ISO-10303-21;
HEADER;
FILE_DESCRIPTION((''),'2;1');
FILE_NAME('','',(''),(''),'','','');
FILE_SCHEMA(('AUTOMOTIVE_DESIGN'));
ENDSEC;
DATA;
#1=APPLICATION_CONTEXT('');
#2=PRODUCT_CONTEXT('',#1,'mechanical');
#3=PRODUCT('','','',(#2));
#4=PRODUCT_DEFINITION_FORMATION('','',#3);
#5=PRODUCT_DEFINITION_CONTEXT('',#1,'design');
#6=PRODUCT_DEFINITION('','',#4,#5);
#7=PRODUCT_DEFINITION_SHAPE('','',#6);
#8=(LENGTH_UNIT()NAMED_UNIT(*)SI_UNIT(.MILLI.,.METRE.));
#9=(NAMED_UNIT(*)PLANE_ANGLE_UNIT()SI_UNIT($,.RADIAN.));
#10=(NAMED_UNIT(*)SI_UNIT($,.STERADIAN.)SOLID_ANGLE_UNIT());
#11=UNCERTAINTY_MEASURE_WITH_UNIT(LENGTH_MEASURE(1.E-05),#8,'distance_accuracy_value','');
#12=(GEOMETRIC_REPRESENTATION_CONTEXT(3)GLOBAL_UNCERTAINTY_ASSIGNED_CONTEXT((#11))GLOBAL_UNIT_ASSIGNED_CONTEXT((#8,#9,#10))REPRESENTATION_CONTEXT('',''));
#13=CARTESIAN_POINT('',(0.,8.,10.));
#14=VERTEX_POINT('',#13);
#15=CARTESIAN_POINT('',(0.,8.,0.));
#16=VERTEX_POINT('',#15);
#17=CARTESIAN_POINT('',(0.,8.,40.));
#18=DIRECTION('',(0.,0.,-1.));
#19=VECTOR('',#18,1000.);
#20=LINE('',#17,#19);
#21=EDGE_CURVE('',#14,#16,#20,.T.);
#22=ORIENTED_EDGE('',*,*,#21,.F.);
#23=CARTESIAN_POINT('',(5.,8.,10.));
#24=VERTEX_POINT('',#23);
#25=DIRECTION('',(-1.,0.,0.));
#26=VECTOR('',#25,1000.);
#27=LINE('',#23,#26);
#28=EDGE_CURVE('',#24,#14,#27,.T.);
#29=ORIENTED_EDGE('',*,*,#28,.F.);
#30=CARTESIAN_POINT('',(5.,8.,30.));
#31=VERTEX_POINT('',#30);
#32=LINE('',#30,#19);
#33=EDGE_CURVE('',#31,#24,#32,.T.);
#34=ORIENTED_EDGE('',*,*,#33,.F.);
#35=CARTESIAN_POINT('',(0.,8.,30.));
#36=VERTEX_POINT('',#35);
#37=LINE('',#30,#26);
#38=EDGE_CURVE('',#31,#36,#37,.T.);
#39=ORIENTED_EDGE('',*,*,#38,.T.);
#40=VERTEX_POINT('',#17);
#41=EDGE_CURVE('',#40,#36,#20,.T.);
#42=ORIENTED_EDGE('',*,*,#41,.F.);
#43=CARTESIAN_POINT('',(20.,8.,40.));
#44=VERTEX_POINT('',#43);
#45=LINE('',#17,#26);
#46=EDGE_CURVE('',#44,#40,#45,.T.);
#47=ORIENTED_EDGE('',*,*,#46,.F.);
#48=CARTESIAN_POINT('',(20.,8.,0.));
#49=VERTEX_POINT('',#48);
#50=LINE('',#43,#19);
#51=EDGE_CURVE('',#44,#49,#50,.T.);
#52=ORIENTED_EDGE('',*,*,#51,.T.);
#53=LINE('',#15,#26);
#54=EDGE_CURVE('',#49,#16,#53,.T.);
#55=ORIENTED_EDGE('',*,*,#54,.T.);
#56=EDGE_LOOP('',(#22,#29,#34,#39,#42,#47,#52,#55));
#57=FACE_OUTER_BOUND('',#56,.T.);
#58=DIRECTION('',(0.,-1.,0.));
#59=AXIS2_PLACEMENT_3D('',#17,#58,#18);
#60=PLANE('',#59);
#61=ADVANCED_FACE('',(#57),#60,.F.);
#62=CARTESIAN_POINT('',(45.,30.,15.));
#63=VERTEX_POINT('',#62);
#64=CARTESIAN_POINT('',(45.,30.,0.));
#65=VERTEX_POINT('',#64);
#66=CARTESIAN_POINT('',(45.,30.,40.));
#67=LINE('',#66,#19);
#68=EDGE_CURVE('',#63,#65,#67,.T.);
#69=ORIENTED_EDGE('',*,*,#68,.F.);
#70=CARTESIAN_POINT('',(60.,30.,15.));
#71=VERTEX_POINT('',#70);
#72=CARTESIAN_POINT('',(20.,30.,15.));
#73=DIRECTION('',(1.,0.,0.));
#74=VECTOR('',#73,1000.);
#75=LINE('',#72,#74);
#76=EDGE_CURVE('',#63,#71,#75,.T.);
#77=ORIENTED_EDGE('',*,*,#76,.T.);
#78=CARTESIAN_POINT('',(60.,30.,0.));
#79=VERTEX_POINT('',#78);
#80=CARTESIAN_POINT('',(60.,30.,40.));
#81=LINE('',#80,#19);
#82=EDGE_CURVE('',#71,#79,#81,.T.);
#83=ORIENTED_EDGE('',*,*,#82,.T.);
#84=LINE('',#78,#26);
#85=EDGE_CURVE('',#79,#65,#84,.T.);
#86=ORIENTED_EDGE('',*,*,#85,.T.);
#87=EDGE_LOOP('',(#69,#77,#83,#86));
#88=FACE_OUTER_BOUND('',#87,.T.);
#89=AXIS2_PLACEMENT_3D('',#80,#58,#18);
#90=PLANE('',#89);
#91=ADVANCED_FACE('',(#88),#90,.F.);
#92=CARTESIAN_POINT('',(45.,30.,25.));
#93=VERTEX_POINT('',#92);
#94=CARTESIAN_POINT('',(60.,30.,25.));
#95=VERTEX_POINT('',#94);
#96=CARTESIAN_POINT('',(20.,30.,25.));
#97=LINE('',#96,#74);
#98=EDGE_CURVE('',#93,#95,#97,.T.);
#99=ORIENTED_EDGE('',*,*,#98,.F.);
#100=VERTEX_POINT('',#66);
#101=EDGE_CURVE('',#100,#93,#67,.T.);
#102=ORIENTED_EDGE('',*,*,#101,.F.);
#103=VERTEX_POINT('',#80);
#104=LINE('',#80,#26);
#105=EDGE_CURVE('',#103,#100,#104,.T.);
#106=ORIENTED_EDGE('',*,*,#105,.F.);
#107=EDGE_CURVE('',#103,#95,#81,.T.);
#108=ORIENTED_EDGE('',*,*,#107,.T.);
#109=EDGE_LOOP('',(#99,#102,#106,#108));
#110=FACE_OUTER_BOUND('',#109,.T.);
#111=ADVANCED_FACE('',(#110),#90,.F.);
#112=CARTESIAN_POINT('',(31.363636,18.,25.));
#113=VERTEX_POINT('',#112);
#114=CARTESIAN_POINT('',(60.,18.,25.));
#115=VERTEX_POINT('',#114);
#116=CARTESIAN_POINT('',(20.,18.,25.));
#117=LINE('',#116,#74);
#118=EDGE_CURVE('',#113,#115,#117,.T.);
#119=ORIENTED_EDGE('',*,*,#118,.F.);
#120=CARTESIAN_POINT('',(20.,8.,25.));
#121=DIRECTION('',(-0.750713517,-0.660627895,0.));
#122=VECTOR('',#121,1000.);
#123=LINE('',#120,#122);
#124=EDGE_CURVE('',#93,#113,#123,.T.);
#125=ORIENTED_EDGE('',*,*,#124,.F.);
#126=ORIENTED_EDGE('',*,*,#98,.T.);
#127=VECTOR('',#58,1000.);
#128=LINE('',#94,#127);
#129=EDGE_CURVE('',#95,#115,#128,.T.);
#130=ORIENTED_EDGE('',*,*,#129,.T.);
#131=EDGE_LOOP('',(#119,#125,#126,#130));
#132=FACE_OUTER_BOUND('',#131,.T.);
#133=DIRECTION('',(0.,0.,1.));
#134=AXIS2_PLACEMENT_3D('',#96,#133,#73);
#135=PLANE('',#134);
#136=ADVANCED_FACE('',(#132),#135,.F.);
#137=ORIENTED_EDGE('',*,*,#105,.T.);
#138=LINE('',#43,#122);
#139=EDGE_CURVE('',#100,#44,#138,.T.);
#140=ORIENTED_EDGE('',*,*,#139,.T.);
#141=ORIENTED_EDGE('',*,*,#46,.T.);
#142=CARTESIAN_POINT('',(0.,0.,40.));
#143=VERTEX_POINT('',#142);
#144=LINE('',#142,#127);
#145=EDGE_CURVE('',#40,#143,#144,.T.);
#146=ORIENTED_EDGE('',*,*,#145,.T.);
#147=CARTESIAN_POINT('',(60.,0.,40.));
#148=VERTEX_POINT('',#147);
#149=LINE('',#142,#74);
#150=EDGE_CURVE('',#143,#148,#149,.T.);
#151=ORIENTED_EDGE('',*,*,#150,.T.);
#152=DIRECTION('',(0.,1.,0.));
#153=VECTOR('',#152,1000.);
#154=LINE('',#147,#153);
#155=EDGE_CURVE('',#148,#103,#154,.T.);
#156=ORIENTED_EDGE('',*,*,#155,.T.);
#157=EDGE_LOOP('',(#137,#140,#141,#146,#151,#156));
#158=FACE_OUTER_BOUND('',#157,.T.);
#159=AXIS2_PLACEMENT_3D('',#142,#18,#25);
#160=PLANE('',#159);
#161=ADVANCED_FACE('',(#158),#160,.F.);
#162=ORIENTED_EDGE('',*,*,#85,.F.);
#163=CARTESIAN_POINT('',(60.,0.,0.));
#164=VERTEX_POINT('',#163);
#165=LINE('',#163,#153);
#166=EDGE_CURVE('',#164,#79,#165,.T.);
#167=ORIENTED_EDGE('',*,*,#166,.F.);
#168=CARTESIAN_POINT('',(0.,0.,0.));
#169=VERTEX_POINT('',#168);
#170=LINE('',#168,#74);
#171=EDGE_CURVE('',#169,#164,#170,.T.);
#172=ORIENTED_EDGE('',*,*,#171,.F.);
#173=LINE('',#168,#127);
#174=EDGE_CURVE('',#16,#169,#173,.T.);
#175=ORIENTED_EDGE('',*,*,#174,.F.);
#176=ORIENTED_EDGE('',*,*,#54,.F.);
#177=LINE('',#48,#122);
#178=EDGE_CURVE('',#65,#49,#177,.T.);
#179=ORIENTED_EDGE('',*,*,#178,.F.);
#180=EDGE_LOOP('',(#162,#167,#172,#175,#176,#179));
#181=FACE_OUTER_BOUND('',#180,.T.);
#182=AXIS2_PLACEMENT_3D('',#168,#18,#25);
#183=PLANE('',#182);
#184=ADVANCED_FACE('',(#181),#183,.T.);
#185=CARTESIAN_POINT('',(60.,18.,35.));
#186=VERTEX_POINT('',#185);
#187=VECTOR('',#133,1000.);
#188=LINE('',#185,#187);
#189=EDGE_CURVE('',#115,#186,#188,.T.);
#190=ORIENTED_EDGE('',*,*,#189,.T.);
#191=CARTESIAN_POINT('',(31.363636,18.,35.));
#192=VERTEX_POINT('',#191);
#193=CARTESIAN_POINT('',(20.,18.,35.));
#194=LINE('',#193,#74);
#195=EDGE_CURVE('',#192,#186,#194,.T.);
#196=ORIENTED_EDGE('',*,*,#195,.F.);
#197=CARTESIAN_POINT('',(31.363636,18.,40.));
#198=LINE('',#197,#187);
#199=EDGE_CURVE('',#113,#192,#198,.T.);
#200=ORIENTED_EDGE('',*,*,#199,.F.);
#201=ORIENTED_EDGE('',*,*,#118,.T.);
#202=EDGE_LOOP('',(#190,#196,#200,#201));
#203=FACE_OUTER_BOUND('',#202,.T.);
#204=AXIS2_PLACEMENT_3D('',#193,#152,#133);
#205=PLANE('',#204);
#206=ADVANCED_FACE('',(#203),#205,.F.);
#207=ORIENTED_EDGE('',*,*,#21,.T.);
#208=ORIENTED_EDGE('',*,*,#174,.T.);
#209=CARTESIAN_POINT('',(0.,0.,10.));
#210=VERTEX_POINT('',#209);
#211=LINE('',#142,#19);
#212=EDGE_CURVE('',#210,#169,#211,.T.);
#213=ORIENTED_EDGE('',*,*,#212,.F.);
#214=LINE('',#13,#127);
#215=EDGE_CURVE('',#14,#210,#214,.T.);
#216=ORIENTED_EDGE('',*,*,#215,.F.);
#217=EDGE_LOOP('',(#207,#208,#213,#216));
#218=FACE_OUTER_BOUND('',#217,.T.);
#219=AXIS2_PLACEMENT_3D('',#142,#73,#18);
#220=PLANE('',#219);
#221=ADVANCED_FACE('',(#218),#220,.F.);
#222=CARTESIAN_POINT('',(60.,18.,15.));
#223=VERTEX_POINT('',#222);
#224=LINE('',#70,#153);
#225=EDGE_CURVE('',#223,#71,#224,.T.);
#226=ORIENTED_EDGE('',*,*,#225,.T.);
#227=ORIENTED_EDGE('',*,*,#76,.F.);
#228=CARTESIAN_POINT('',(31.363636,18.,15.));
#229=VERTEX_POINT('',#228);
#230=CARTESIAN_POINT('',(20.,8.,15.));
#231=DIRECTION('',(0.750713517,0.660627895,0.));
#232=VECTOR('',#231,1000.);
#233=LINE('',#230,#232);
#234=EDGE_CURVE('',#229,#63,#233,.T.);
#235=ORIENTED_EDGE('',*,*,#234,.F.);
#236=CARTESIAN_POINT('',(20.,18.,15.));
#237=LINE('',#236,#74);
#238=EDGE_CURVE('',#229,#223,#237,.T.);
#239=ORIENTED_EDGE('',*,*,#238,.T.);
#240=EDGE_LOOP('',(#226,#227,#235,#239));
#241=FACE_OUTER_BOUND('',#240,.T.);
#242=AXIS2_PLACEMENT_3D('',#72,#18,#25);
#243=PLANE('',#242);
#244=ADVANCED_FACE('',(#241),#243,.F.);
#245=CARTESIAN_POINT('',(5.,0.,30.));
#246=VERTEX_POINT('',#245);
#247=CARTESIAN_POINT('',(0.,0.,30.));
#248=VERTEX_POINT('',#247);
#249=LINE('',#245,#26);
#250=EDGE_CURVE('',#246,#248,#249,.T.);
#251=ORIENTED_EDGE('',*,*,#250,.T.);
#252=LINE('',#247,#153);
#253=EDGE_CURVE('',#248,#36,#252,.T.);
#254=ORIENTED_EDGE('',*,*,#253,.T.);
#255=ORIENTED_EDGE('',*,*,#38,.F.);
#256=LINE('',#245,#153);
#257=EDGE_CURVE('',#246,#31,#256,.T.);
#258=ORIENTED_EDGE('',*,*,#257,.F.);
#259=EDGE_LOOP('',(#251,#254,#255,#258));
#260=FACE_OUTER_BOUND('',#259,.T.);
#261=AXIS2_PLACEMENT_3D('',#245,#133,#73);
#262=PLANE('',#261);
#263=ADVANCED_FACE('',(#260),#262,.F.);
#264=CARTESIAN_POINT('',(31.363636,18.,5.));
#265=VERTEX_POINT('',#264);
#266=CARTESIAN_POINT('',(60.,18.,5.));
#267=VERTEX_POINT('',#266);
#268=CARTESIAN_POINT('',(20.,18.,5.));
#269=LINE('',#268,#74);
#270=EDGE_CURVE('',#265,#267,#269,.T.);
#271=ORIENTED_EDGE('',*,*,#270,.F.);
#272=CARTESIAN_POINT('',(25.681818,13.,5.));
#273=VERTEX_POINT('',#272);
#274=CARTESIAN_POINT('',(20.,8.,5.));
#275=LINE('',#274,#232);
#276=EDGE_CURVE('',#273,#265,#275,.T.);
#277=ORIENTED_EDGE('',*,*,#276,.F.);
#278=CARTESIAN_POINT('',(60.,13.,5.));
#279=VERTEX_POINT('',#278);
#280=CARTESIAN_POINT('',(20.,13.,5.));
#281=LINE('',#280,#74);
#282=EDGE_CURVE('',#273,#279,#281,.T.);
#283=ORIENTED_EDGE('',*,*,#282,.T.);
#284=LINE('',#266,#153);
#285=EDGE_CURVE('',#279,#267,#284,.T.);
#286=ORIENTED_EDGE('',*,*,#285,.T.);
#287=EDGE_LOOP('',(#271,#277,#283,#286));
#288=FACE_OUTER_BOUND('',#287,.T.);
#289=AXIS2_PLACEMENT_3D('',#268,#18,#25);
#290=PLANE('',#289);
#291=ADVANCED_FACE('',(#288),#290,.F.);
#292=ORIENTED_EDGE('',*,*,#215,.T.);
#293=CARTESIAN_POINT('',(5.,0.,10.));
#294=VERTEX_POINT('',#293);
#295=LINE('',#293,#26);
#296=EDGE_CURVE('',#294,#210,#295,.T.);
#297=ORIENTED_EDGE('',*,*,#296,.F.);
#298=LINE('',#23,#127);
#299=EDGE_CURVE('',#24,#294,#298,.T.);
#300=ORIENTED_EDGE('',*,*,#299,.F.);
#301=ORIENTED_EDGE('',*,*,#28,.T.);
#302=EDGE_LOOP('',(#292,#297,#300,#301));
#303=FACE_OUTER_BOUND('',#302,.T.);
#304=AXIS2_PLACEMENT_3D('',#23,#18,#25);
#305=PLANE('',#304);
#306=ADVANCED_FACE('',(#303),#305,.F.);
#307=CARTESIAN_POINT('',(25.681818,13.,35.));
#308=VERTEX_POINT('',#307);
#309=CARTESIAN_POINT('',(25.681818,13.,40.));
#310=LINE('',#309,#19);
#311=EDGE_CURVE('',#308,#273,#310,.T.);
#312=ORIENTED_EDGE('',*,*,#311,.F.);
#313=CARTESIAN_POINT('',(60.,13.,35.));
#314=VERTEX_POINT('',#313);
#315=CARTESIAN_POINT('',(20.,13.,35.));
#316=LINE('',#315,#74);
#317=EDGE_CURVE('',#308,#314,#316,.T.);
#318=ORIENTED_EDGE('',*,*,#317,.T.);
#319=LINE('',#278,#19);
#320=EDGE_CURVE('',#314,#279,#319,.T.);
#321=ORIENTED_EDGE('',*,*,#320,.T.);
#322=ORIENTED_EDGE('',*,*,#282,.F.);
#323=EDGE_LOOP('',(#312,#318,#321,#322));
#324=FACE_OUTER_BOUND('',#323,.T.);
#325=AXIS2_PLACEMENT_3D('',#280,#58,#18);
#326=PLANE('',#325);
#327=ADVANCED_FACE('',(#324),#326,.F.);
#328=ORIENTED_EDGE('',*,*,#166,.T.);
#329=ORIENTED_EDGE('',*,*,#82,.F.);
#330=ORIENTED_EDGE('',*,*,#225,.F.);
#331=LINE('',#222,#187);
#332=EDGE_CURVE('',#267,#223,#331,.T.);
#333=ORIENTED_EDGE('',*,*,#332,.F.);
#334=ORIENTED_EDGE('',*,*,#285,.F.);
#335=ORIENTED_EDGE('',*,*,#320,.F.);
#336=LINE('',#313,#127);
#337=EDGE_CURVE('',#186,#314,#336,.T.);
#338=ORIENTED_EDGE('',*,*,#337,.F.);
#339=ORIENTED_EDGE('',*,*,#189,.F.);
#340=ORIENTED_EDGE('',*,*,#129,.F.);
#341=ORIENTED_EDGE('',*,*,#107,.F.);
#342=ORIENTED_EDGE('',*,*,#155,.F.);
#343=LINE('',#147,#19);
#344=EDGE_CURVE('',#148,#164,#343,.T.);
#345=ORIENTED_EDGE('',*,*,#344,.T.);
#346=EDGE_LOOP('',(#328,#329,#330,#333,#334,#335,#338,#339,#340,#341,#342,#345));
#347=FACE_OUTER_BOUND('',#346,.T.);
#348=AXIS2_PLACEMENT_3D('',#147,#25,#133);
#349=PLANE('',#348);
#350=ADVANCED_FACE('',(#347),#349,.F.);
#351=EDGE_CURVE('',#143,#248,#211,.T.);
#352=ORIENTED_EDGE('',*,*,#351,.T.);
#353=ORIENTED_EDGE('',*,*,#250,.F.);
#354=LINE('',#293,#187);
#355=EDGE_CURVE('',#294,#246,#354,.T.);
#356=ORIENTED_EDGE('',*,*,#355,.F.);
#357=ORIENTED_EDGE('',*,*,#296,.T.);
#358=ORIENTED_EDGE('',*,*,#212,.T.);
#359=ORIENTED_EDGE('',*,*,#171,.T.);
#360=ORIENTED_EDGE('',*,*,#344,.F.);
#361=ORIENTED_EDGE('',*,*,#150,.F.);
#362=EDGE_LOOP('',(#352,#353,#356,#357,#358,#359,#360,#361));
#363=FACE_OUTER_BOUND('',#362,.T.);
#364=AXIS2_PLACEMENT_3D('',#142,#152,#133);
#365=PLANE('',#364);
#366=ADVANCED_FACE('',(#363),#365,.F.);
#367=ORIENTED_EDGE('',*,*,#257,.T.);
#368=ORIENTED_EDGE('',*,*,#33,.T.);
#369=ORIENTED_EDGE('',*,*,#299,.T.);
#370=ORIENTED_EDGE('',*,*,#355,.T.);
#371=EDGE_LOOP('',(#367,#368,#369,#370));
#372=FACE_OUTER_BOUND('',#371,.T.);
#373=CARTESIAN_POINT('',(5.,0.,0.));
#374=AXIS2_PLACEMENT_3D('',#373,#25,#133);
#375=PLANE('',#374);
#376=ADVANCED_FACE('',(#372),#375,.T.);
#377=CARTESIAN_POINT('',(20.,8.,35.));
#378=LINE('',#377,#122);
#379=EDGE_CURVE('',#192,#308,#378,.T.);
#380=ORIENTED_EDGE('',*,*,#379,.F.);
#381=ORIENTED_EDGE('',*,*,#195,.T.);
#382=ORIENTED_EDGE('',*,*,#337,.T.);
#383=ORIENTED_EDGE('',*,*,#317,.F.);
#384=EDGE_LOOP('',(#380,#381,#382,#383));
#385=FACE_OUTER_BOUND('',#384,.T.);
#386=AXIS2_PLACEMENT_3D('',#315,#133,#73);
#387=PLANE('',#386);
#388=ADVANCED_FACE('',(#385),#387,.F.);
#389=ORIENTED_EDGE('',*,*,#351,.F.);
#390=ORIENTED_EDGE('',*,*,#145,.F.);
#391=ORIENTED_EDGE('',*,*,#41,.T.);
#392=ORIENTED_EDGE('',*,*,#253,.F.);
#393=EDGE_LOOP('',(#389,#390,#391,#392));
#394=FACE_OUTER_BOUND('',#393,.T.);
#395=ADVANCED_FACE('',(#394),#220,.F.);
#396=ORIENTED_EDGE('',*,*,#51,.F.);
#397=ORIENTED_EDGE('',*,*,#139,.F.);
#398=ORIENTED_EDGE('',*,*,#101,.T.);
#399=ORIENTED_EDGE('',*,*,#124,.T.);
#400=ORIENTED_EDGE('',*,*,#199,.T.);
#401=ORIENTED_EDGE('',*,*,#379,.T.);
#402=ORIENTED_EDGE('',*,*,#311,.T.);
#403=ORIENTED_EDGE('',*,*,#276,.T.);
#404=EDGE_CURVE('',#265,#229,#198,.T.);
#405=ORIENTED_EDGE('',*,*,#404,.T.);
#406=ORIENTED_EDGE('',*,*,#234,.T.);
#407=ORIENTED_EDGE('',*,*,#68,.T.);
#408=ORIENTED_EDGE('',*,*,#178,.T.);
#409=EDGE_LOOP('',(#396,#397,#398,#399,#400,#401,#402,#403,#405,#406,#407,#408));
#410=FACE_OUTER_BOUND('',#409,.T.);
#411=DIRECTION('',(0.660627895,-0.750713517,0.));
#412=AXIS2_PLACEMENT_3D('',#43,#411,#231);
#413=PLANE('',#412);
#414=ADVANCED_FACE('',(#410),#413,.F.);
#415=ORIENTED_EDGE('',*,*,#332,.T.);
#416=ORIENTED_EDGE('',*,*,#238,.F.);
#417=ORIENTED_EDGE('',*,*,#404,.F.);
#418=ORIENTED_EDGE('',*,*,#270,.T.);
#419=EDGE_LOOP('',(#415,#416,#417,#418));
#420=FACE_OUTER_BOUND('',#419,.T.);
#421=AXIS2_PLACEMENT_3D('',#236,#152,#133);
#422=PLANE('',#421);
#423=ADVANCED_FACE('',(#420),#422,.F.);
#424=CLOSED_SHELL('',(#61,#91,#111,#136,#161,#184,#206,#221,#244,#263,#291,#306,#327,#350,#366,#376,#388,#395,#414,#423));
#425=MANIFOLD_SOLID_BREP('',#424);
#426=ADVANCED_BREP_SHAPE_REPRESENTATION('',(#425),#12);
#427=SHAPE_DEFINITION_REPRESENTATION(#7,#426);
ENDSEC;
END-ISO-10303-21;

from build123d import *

# Parameters (mm, degrees)
ANGLED_BASE_BLOCK_DEPTH  = 40
GROOVE_CUT_5MM_DEPTH     = 5
T_SLOT_THROUGH_CUT_DEPTH = 40


with BuildPart() as part:
    # Base Profile Sketch → Angled Base Block (new body)
    with BuildSketch(Plane.XY):
        Polygon((0, 0), (60, 0), (60, 30), (45, 30), (20, 8), (0, 8), align=None)
    extrude(amount=ANGLED_BASE_BLOCK_DEPTH)

    # Groove Profile Sketch → Groove Cut 5mm (cut)
    with BuildSketch(Plane.ZY):
        Polygon((20, 8), (10, 8), (10, 0), (30, 0), (30, 8), align=None)
    extrude(amount=-GROOVE_CUT_5MM_DEPTH, mode=Mode.SUBTRACT)

    # T-Slot Profile Sketch → T-Slot Through Cut (cut)
    with BuildSketch(Plane(origin=(60, 0, 0), x_dir=(0, 0, -1), z_dir=(1, 0, 0))):
        Polygon((-20, 30), (-25, 30), (-25, 18), (-35, 18), (-35, 13), (-5, 13), (-5, 18), (-15, 18), (-15, 30), align=None)
    extrude(amount=-T_SLOT_THROUGH_CUT_DEPTH, mode=Mode.SUBTRACT)


solid = part.part
